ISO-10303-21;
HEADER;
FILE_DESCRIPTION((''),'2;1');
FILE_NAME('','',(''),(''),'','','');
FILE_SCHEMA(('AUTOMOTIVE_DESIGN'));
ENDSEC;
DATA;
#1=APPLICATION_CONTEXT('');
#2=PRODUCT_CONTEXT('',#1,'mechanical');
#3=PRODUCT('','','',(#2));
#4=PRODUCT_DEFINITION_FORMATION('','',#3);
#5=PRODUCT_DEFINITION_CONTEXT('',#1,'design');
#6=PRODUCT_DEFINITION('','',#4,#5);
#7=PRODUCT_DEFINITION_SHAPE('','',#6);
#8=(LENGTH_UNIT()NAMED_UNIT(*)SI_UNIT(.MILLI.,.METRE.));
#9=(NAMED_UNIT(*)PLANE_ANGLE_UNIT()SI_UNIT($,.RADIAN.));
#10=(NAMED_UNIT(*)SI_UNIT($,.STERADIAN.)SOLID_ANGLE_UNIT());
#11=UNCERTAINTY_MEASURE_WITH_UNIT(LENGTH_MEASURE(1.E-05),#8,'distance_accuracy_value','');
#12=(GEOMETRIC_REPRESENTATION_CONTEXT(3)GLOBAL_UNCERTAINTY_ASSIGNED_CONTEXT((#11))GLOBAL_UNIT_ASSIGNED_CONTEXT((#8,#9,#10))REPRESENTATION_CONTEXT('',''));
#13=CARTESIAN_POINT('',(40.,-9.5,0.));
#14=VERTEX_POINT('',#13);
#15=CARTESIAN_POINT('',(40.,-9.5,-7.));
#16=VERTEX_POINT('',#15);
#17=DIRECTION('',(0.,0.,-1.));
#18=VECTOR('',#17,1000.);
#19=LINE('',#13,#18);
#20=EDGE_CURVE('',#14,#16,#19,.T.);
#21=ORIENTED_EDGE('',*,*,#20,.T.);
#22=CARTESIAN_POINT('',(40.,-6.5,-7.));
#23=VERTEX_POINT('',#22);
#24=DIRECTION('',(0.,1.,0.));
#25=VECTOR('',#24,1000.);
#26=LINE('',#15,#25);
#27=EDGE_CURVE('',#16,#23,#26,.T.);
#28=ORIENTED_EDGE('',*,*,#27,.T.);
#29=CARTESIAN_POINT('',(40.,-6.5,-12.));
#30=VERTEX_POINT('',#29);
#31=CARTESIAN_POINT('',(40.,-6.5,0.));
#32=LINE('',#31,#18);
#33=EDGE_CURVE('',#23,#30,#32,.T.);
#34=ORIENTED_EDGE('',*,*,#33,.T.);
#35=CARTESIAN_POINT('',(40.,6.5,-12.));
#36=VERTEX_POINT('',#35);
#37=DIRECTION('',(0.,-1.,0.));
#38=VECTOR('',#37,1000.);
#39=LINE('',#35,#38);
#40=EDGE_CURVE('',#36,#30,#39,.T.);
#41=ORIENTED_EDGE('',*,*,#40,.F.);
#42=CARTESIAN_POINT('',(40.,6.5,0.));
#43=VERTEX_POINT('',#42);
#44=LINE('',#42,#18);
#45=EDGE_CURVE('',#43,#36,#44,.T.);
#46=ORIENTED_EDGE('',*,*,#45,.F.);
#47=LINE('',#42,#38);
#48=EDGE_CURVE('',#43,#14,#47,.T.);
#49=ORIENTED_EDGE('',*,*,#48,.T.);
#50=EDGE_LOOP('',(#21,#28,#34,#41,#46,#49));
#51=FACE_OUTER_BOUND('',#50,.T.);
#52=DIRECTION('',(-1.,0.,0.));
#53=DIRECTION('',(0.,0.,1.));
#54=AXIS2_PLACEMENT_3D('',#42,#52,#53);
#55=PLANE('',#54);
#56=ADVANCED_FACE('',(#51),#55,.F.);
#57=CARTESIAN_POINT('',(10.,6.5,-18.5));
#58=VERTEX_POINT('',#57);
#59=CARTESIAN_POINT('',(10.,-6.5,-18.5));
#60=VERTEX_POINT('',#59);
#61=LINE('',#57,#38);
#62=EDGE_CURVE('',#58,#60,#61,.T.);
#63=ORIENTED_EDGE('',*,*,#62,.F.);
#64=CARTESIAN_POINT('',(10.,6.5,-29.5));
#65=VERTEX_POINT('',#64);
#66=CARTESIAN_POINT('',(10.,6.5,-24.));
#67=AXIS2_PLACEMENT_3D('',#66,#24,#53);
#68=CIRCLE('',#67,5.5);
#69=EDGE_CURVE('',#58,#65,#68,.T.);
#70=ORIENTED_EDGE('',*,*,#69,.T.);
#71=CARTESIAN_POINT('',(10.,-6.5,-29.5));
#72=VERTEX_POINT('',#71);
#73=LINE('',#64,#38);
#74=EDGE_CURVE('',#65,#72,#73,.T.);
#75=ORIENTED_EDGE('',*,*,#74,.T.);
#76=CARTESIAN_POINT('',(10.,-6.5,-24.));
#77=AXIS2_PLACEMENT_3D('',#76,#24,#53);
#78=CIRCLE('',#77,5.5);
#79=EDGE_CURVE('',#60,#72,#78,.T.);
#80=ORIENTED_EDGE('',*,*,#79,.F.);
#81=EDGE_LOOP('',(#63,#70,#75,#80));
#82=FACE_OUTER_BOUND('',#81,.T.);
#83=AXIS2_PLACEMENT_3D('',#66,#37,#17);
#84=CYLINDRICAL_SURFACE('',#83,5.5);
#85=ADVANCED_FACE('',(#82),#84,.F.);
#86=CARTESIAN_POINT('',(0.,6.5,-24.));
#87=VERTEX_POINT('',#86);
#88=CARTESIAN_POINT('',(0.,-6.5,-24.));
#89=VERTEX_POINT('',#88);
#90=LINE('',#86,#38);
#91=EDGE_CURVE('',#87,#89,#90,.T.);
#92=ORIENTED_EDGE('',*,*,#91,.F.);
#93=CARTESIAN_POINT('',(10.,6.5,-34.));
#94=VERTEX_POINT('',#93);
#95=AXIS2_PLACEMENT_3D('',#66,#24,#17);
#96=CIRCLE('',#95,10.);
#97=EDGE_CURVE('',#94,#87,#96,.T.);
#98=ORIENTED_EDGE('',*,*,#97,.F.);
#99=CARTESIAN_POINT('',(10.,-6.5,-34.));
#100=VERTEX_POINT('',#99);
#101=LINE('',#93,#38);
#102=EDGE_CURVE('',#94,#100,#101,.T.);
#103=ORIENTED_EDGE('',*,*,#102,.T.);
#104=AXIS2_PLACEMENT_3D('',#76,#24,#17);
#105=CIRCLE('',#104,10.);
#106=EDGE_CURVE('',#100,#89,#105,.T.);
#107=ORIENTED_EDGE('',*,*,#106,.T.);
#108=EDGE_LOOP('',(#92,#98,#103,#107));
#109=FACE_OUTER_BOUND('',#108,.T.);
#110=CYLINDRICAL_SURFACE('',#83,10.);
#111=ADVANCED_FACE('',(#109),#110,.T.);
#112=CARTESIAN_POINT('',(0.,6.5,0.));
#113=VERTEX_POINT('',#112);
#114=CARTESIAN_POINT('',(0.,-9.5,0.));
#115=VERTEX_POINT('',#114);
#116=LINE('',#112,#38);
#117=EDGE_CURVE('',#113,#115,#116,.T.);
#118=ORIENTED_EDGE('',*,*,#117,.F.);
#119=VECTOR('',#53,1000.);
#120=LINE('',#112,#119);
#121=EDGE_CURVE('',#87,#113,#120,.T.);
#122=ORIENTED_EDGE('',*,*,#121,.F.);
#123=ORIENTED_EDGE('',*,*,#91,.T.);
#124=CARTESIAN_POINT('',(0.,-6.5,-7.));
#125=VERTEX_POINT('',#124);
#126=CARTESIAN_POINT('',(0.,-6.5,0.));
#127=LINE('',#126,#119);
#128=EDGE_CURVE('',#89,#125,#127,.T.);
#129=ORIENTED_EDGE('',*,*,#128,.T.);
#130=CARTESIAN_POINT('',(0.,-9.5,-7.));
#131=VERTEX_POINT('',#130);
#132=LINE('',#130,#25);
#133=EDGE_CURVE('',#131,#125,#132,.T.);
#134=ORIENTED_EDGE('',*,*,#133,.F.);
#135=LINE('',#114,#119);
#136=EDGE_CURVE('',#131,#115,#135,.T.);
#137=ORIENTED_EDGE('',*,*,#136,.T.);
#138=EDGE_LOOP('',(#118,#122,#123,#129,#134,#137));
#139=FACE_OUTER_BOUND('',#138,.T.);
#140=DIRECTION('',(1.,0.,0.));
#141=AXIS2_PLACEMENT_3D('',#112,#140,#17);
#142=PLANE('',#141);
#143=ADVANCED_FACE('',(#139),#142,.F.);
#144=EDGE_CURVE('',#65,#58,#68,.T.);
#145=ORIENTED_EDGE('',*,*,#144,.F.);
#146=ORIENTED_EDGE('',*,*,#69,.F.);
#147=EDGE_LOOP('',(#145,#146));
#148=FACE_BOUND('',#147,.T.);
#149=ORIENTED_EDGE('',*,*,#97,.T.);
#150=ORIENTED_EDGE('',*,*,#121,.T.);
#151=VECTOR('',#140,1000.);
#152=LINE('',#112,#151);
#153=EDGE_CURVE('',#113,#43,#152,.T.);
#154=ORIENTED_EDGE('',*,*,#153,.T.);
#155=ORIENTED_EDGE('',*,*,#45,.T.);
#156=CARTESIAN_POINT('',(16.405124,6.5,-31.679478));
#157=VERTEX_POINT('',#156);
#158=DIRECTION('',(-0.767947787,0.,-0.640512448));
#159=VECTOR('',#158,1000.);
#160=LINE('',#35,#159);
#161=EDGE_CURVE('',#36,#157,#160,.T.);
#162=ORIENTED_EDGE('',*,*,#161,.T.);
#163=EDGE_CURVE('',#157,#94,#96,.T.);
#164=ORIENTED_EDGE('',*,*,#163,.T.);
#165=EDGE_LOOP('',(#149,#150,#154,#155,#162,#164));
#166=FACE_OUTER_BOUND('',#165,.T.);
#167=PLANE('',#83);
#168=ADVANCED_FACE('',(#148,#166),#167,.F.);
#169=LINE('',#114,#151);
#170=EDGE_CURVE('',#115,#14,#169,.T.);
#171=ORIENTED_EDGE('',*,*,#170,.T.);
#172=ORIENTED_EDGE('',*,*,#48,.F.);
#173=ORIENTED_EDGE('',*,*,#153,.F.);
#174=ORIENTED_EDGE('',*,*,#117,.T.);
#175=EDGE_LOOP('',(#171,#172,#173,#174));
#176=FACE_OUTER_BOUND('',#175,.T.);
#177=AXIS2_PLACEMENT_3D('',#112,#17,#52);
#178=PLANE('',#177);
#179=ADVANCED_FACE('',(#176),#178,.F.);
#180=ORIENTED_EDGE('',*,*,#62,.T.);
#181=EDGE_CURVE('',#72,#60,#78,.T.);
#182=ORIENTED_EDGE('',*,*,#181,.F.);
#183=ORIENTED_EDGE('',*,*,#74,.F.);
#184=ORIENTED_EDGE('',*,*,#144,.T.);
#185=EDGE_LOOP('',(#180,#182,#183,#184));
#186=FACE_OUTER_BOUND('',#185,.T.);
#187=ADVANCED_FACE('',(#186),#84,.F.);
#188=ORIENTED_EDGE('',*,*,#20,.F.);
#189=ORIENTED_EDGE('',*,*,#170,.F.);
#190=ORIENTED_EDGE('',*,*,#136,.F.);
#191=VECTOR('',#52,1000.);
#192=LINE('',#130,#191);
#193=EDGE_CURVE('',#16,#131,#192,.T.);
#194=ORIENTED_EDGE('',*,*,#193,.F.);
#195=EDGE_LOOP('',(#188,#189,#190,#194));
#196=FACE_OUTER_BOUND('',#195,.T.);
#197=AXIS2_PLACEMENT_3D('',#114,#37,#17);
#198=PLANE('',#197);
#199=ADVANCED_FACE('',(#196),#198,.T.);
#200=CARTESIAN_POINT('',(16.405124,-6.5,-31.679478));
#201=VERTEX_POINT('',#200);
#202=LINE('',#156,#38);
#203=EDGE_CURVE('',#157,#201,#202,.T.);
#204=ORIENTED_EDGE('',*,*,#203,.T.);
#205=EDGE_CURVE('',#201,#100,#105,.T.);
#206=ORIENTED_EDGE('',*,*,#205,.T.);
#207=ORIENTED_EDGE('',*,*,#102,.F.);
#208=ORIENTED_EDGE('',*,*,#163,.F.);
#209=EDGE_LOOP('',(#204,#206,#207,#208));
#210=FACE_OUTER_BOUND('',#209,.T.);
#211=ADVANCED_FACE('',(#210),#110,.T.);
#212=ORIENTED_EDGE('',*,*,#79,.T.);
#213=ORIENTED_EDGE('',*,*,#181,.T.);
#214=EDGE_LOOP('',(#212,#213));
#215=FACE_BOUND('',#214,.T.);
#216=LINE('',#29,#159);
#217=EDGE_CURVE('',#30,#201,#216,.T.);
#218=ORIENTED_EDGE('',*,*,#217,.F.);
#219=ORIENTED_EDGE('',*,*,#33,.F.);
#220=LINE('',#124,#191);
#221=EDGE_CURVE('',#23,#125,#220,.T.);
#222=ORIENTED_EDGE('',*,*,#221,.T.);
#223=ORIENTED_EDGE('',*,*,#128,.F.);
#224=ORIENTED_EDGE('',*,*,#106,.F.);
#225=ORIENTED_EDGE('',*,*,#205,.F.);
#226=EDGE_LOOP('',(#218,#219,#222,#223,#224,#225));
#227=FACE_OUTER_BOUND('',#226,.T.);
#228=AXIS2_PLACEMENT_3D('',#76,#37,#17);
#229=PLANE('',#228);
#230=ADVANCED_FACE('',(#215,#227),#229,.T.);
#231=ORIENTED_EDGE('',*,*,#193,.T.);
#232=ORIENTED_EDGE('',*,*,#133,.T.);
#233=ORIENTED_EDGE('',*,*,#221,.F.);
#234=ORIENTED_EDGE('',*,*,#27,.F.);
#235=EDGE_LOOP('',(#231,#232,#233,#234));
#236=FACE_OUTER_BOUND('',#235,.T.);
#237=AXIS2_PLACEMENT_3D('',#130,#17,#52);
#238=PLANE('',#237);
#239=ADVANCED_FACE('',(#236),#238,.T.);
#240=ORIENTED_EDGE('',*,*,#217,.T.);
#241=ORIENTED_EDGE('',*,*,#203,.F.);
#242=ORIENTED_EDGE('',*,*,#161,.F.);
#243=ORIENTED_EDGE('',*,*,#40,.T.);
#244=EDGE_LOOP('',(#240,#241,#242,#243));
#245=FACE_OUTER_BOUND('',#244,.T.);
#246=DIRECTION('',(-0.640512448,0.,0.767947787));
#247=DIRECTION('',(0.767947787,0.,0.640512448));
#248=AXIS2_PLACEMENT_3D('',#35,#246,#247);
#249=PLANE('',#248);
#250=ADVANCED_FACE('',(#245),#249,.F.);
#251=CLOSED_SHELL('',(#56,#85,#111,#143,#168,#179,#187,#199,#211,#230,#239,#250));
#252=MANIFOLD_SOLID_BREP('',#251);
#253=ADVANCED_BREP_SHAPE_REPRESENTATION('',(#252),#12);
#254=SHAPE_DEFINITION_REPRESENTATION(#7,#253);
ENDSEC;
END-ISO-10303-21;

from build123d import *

# Parameters (mm, degrees)
SKETCH1_R           = 5.5
BOSS_EXTRUDE1_DEPTH = 6.5
SKETCH2_W           = 40
SKETCH2_H           = 7
BOSS_EXTRUDE2_DEPTH = 3


with BuildPart() as part:
    # Sketch1 → Boss-Extrude1 (new, symmetric)
    with BuildSketch(Plane(origin=(0, 0, 0), x_dir=(1, 0, 0), z_dir=(0, 1, 0))):
        with BuildLine():
            Line((40, 12), (16.405124482, 31.679477871))
            ThreePointArc((16.405124482, 31.679477871), (5.760380018, 33.056799788), (0, 24))
            Line((0, 24), (0, 0))
            Line((0, 0), (40, 0))
            Line((40, 0), (40, 12))
        make_face()
        with Locations(Location((10, 24, 0), (0, 0, 90))):
            Circle(SKETCH1_R, mode=Mode.SUBTRACT)
    extrude(amount=BOSS_EXTRUDE1_DEPTH, both=True)

    # Sketch2 → Boss-Extrude2 (add)
    with BuildSketch(Plane(origin=(0, -6.5, 0), x_dir=(1, 0, 0), z_dir=(0, 1, 0))):
        with Locations((20, 3.5)):
            Rectangle(SKETCH2_W, SKETCH2_H)
    extrude(amount=-BOSS_EXTRUDE2_DEPTH)


solid = part.part
